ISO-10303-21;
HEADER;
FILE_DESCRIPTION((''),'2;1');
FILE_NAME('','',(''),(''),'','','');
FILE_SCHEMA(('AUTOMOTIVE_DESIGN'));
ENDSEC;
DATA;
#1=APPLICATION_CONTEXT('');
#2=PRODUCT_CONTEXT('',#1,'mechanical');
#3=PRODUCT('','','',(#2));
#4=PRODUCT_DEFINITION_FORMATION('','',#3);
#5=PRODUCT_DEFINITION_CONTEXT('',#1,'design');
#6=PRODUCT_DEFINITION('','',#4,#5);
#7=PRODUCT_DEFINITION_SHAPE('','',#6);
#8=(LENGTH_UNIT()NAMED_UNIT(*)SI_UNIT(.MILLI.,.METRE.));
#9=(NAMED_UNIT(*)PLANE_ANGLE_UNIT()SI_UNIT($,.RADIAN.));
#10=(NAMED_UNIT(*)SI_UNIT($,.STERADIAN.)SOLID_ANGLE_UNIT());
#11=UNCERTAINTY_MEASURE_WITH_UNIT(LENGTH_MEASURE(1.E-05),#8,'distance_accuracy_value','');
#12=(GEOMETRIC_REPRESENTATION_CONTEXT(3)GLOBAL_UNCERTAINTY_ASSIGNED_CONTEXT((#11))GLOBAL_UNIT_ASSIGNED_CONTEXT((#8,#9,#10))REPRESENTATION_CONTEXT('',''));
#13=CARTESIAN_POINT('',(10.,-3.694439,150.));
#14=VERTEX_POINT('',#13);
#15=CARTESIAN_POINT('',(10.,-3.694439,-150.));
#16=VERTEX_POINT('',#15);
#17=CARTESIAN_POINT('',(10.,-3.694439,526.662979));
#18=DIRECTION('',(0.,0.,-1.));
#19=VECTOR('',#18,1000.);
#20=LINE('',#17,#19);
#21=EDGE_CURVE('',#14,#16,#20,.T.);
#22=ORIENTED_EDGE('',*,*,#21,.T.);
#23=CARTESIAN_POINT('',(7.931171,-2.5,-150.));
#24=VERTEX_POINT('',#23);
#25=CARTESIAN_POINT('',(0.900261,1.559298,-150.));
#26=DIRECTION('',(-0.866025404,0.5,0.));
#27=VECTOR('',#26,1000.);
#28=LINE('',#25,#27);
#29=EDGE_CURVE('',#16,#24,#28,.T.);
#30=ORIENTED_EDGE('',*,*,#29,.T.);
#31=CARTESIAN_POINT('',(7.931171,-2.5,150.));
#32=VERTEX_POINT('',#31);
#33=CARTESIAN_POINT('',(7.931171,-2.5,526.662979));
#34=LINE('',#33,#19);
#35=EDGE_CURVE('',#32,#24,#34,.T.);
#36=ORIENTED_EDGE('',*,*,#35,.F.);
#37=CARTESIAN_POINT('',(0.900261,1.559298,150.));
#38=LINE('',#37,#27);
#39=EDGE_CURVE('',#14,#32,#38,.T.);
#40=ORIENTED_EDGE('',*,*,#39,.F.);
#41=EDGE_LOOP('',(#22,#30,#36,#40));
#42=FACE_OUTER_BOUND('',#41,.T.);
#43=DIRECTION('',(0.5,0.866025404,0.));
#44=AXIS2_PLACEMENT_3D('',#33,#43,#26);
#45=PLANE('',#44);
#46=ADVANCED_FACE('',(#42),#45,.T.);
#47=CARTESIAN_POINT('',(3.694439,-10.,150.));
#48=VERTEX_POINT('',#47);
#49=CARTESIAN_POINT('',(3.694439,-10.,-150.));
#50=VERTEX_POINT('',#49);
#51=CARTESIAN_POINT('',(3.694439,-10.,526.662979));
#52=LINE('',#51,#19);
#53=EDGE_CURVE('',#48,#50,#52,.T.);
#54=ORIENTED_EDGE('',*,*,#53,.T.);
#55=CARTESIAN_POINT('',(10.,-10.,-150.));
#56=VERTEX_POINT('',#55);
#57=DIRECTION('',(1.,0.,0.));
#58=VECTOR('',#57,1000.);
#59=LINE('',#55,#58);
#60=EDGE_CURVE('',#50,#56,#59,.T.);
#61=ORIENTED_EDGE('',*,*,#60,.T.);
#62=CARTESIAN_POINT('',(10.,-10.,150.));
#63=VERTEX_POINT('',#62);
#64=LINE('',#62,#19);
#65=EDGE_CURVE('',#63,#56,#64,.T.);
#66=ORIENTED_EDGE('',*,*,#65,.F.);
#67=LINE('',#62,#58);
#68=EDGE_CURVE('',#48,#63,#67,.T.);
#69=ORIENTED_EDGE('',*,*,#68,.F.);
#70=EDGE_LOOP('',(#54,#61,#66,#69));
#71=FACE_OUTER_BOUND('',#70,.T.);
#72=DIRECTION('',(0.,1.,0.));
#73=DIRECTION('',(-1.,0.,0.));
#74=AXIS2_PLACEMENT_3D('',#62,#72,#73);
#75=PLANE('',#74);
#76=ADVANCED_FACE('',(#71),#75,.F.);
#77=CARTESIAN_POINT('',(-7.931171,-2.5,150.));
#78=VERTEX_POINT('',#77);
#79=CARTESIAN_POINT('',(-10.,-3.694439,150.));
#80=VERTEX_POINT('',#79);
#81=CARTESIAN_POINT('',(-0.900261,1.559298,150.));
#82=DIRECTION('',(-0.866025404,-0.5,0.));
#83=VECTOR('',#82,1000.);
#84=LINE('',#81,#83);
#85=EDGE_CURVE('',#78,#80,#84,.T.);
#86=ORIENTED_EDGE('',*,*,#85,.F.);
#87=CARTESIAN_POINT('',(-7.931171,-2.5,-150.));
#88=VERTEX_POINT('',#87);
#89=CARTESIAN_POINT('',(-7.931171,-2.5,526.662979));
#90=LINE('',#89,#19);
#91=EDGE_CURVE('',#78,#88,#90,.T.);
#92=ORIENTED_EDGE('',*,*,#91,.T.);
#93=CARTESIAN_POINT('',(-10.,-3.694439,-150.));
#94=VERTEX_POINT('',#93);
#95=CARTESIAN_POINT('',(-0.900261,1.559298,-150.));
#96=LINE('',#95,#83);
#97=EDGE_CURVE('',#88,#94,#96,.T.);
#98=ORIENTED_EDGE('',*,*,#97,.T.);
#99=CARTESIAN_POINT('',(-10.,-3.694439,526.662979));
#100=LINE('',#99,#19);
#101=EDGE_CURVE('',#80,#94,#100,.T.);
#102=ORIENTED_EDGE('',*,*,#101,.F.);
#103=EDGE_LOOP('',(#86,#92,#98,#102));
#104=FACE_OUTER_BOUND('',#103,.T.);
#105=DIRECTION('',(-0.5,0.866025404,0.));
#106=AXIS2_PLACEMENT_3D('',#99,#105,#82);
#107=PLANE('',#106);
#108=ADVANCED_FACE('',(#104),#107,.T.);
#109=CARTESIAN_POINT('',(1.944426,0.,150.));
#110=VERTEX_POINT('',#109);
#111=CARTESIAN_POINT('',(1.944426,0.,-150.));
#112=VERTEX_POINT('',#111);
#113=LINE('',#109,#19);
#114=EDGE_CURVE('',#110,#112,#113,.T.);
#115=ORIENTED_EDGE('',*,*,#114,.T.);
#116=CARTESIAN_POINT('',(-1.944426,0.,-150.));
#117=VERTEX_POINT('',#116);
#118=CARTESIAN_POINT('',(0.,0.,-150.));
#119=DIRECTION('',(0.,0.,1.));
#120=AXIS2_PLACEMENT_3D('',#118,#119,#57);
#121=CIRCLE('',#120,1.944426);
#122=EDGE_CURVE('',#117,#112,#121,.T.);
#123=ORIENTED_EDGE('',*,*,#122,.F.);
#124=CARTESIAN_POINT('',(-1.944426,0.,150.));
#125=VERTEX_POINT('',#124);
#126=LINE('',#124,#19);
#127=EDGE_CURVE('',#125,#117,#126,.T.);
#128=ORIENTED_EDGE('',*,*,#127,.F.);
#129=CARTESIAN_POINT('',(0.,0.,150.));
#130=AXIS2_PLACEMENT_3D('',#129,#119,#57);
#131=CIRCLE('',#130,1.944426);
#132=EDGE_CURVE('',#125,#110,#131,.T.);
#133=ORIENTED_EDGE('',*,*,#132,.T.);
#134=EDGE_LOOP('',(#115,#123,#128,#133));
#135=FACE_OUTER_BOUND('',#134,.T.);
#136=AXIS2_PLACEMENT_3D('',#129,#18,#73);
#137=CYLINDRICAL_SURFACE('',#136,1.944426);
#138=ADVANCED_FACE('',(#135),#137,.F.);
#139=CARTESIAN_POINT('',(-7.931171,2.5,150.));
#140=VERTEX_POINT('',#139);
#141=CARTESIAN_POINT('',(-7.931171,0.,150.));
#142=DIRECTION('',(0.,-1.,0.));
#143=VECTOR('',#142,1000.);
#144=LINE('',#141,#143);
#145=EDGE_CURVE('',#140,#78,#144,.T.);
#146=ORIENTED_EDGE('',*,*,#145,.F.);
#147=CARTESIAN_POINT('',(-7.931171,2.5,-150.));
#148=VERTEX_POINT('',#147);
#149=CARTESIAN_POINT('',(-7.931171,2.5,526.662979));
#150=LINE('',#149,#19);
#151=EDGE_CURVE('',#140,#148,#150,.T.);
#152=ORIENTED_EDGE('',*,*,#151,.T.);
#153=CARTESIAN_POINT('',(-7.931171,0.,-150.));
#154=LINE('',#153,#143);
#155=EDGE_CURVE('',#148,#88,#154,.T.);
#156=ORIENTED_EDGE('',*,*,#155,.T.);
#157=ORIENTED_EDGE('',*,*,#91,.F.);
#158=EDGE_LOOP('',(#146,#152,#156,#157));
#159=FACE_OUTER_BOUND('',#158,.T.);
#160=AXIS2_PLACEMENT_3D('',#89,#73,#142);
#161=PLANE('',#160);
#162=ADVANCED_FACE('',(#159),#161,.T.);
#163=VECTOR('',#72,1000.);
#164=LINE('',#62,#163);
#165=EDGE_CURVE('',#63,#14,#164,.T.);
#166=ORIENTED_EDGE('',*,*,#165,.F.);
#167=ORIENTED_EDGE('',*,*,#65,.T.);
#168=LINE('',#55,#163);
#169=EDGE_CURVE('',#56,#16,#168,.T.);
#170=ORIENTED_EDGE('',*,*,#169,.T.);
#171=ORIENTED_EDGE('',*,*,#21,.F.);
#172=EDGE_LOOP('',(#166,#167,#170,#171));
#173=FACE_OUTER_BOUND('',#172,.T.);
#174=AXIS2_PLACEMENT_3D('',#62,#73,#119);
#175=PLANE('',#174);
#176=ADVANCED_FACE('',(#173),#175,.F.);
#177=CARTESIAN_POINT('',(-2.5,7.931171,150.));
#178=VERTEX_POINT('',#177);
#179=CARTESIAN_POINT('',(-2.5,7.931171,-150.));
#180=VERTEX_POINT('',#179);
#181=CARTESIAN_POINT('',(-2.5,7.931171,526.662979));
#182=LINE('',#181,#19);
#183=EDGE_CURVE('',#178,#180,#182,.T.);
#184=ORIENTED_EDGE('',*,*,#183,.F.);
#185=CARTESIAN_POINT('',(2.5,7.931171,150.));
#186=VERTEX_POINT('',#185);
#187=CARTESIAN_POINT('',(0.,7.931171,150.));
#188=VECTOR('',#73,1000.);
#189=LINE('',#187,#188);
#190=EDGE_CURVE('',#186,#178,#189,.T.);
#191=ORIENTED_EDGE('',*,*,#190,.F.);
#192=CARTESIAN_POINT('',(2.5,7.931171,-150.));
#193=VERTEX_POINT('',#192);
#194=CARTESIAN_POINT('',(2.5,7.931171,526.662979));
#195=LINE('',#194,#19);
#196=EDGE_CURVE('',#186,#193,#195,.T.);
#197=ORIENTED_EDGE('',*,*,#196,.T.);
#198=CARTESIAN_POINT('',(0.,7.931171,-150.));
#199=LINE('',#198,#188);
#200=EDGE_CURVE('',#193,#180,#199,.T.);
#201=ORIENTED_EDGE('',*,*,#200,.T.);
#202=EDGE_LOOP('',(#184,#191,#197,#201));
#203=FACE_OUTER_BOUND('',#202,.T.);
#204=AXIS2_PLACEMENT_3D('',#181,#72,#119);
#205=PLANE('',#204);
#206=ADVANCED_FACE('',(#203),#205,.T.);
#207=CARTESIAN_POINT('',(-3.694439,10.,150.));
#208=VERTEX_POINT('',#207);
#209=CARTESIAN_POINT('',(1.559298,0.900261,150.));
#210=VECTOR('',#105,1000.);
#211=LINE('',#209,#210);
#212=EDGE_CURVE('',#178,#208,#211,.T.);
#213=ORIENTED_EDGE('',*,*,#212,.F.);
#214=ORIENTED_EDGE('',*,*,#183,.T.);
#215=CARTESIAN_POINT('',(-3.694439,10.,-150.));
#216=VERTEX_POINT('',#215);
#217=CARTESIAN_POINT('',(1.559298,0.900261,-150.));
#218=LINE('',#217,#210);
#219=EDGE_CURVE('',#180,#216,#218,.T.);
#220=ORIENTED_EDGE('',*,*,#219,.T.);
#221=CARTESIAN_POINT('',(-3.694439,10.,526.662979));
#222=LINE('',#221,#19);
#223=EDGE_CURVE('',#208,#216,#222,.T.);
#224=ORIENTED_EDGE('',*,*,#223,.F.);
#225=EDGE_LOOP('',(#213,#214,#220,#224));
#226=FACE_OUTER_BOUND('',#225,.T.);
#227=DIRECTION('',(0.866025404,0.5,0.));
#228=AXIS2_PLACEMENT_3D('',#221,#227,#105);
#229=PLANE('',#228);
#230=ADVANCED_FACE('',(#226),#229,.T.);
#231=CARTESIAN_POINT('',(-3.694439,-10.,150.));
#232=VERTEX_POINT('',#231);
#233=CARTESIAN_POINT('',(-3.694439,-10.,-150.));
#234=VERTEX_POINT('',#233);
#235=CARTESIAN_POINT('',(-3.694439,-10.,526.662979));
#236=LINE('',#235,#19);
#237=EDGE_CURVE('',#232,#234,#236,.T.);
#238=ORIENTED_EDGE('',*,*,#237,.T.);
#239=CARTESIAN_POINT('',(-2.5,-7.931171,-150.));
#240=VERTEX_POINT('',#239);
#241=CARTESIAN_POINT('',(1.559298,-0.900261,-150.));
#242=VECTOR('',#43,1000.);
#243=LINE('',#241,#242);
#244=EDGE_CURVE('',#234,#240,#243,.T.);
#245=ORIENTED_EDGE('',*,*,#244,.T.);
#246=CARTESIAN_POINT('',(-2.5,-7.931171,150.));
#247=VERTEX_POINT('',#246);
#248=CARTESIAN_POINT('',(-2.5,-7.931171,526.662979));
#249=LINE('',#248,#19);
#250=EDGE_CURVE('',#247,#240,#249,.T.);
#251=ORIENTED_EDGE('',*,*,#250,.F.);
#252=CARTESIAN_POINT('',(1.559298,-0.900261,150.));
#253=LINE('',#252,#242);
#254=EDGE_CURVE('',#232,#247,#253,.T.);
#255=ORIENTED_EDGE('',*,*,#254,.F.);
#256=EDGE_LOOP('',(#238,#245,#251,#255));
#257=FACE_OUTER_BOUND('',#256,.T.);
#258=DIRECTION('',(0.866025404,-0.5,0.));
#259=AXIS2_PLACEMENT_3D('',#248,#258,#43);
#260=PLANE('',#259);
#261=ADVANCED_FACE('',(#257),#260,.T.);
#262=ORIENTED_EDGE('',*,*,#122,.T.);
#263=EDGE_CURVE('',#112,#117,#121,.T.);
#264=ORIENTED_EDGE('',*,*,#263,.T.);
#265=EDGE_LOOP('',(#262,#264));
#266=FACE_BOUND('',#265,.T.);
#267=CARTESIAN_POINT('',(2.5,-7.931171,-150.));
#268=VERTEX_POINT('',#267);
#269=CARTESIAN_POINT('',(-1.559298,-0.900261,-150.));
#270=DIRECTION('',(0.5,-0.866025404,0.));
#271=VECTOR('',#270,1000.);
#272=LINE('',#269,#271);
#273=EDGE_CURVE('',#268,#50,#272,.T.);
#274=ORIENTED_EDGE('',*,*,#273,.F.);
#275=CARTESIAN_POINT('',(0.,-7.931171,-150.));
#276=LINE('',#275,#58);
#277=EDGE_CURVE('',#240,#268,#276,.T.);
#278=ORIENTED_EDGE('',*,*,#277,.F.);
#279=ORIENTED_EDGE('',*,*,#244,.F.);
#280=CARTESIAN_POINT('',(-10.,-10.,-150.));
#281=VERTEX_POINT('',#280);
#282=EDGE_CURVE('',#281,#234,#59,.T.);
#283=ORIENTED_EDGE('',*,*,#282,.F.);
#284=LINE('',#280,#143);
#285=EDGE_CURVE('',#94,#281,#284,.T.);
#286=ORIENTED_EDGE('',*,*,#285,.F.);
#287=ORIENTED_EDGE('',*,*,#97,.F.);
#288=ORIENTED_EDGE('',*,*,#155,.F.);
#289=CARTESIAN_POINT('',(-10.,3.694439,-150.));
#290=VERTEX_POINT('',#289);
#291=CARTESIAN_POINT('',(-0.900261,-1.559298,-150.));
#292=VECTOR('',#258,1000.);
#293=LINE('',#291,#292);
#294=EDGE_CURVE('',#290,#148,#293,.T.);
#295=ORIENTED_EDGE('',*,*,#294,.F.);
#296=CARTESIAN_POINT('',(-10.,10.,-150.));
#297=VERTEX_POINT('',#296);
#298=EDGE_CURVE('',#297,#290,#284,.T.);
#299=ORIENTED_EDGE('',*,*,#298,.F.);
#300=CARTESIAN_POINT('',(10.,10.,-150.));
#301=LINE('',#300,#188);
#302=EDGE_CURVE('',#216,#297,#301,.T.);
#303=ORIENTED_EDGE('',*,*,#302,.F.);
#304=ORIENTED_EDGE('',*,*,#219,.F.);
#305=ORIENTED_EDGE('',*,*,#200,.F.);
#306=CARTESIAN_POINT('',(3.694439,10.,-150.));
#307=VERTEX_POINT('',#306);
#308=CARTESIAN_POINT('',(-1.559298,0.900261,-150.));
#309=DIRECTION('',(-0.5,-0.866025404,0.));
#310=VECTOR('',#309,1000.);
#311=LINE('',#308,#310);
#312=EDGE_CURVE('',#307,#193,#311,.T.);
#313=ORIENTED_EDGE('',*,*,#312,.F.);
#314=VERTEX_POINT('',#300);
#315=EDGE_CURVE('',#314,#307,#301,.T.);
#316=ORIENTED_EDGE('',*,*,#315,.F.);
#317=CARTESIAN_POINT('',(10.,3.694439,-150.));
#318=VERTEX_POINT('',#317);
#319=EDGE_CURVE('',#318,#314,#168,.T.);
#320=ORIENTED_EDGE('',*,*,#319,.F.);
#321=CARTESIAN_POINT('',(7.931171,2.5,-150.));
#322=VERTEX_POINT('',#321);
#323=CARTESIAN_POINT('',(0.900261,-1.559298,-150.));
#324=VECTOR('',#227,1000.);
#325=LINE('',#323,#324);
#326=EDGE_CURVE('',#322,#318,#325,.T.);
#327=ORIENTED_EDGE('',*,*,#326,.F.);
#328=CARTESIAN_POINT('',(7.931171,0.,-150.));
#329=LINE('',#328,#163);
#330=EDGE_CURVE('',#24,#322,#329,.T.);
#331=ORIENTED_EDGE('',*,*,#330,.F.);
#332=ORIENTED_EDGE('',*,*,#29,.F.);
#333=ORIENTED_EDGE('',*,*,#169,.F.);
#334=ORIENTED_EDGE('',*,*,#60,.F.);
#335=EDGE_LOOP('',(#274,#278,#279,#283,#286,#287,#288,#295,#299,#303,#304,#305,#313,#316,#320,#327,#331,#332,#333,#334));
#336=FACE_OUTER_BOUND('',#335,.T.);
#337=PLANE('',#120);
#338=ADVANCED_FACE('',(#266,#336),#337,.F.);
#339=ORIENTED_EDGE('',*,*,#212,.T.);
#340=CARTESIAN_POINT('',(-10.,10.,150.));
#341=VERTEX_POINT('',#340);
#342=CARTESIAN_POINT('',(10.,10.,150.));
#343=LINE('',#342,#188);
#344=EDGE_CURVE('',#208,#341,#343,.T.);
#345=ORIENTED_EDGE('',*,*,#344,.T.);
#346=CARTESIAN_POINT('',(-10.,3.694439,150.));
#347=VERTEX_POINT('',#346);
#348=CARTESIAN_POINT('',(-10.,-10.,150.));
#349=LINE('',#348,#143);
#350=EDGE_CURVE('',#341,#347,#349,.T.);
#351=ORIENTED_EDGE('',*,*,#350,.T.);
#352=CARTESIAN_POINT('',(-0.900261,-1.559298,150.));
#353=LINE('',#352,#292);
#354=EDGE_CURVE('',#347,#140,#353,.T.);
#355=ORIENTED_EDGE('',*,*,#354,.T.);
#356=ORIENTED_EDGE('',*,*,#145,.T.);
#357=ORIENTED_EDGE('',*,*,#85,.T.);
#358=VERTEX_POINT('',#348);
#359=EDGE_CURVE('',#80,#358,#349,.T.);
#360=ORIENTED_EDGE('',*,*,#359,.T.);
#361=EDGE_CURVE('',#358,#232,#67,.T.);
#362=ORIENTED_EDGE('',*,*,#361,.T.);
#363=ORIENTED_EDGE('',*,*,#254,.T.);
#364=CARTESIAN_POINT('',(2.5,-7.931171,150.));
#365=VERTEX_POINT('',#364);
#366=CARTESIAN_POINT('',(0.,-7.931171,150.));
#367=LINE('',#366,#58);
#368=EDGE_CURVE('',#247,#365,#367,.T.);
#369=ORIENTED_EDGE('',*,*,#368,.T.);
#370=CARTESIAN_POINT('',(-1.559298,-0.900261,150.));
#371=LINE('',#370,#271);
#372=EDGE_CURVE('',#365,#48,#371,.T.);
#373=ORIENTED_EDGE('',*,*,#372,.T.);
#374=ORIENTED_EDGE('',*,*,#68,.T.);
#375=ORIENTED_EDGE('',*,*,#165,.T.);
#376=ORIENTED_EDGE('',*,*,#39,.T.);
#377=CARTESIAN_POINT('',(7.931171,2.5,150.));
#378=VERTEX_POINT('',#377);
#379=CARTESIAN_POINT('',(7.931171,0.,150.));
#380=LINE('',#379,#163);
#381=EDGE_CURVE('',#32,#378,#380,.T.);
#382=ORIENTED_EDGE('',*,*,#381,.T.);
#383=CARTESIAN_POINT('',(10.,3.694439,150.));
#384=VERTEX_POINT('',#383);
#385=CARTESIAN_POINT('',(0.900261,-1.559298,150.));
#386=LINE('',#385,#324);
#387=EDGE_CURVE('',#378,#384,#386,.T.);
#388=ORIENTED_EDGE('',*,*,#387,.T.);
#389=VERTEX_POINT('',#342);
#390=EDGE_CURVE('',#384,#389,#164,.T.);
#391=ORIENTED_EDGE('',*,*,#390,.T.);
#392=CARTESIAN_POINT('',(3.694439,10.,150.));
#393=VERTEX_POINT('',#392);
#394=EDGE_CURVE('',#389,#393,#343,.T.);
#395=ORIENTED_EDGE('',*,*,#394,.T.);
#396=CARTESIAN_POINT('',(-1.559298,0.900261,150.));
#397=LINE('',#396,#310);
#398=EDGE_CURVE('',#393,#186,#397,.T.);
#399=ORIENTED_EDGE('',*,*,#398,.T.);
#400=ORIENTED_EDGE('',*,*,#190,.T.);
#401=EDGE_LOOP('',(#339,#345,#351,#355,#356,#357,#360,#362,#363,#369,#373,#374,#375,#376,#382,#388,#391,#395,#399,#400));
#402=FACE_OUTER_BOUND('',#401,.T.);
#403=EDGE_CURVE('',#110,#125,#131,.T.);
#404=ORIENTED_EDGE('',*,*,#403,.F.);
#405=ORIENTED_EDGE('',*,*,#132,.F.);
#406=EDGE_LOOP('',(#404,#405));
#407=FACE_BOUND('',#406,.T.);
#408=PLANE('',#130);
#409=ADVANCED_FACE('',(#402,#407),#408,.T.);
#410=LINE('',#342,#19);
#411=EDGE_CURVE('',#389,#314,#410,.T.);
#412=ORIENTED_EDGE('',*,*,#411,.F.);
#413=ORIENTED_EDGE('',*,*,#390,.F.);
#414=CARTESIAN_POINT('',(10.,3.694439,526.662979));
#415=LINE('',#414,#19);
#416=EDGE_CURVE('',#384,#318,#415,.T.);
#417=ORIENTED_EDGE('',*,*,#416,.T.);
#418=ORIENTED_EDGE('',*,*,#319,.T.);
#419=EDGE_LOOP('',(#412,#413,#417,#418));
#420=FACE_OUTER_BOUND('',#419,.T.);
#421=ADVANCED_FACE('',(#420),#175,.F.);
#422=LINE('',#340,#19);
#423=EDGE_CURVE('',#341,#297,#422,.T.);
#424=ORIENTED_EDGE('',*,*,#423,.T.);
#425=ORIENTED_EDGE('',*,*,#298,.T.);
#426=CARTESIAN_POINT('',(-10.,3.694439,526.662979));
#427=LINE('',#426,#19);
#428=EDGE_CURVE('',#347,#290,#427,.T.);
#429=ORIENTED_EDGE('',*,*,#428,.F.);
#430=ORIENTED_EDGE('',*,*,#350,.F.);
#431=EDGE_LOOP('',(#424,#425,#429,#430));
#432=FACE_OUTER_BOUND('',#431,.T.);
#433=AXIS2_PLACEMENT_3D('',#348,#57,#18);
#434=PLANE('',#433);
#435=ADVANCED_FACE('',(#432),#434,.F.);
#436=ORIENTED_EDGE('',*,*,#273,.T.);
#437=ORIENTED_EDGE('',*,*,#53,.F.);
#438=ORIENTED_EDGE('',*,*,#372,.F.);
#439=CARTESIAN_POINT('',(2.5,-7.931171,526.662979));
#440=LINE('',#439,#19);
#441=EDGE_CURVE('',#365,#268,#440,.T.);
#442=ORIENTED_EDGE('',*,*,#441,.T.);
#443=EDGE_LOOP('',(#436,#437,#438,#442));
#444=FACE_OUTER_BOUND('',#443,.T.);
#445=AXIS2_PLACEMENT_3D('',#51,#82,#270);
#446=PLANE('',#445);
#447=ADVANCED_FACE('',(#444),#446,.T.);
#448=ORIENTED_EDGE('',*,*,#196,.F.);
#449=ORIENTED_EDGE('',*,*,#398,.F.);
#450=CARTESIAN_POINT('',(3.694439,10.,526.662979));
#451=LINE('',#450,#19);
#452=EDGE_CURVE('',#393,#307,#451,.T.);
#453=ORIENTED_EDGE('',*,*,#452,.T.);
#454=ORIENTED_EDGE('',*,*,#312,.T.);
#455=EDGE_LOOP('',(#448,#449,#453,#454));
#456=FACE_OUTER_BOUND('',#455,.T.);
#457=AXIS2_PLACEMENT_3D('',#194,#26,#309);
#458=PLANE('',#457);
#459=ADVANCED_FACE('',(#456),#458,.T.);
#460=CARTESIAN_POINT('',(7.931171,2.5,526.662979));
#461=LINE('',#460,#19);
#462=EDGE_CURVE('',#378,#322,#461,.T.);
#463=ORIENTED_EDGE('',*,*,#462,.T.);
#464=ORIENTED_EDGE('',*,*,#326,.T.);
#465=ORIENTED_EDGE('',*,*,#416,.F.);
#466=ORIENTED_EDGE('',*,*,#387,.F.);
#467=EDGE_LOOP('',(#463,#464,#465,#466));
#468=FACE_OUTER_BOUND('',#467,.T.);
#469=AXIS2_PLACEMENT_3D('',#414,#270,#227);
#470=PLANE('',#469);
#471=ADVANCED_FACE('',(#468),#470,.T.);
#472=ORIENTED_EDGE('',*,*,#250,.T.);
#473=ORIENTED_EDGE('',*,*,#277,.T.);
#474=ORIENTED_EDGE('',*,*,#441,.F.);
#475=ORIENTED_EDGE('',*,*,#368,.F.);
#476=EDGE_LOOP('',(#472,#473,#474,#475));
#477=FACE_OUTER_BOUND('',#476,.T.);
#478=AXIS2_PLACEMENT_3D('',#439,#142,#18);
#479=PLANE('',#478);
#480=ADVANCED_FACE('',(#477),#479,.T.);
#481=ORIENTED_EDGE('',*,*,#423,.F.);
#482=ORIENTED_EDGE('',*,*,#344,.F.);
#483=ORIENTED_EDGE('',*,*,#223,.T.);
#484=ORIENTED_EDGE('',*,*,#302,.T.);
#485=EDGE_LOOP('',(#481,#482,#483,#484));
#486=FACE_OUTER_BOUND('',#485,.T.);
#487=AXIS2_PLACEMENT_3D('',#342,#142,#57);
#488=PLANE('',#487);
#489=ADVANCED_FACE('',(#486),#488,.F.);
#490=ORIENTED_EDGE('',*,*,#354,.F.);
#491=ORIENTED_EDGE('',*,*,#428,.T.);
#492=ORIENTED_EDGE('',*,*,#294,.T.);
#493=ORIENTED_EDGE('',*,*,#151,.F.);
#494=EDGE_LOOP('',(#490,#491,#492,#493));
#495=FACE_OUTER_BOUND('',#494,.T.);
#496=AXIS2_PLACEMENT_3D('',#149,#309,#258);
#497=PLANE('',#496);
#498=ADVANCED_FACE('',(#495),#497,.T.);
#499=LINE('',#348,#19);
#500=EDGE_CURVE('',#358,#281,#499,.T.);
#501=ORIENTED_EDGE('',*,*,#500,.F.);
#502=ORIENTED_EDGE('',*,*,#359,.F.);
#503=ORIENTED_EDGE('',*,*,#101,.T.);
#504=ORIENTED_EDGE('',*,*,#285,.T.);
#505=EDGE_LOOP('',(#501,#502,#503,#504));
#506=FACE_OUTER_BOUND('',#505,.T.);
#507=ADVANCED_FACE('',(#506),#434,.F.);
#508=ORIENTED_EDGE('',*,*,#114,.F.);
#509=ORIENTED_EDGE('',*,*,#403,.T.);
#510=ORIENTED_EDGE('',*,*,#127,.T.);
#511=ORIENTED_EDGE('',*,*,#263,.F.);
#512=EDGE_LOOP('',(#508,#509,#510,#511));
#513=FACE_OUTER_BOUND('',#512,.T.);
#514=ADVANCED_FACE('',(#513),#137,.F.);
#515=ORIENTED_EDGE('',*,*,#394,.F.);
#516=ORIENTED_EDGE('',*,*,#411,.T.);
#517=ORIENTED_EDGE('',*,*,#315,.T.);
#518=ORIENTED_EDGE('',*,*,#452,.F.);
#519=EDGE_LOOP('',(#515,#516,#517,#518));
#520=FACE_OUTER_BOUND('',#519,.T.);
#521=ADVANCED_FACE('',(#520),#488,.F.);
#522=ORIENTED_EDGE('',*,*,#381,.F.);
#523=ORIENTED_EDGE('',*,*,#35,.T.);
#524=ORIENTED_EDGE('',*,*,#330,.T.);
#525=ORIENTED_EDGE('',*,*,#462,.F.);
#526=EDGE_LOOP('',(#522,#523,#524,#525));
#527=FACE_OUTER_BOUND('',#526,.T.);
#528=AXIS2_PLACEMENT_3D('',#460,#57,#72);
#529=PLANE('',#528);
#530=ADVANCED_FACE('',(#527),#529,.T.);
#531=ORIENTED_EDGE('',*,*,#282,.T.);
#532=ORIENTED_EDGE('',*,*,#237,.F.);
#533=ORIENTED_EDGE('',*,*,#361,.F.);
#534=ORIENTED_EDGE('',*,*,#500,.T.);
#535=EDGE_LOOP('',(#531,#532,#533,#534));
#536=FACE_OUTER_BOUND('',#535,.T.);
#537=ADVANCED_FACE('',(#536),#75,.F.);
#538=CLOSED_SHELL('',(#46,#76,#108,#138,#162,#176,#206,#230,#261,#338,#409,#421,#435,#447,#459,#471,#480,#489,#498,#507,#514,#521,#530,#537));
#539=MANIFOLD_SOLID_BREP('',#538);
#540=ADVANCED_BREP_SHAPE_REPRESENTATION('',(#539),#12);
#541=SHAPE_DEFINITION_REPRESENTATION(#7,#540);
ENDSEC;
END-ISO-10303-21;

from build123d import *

# Parameters (mm, degrees)
SKETCH_1_W               = 20
SKETCH_1_H               = 20
SKETCH_1_R               = 1.94442565
EXTRUDE_1_DEPTH          = 150
CUT_EXTRUDE_1_DEPTH      = 301.333148354
PATTERN_CIRCULAR_1_COUNT = 4


with BuildPart() as part:
    # 草图1 → 凸台-拉伸1 (new, symmetric)
    with BuildSketch(Plane.XY):
        Rectangle(SKETCH_1_W, SKETCH_1_H)
        Circle(SKETCH_1_R, mode=Mode.SUBTRACT)
    extrude(amount=EXTRUDE_1_DEPTH, both=True)

    # 草图2 → 切除-拉伸1 (cut, symmetric)
    with BuildSketch(Plane.XY.offset(150)):
        Polygon((-32.933615203, 60.643738676), (-3.694439046, 10), (-2.5, 7.931170886), (2.5, 7.931170886), (3.694439046, 10), (32.933615203, 60.643738676), (32.933615203, 177.600443305), (-32.933615203, 177.600443305), align=None)
    cut_extrude_1 = extrude(amount=CUT_EXTRUDE_1_DEPTH, both=True, mode=Mode.SUBTRACT)

    # 阵列(圆周)1: 切除-拉伸1 ×4 about axis
    pattern_circular_1_axis = Axis((0, 0, 150), (0, 0, -1))
    for i in range(1, PATTERN_CIRCULAR_1_COUNT):
        add(cut_extrude_1.rotate(pattern_circular_1_axis, i * 360 / PATTERN_CIRCULAR_1_COUNT), mode=Mode.SUBTRACT)


solid = part.part
